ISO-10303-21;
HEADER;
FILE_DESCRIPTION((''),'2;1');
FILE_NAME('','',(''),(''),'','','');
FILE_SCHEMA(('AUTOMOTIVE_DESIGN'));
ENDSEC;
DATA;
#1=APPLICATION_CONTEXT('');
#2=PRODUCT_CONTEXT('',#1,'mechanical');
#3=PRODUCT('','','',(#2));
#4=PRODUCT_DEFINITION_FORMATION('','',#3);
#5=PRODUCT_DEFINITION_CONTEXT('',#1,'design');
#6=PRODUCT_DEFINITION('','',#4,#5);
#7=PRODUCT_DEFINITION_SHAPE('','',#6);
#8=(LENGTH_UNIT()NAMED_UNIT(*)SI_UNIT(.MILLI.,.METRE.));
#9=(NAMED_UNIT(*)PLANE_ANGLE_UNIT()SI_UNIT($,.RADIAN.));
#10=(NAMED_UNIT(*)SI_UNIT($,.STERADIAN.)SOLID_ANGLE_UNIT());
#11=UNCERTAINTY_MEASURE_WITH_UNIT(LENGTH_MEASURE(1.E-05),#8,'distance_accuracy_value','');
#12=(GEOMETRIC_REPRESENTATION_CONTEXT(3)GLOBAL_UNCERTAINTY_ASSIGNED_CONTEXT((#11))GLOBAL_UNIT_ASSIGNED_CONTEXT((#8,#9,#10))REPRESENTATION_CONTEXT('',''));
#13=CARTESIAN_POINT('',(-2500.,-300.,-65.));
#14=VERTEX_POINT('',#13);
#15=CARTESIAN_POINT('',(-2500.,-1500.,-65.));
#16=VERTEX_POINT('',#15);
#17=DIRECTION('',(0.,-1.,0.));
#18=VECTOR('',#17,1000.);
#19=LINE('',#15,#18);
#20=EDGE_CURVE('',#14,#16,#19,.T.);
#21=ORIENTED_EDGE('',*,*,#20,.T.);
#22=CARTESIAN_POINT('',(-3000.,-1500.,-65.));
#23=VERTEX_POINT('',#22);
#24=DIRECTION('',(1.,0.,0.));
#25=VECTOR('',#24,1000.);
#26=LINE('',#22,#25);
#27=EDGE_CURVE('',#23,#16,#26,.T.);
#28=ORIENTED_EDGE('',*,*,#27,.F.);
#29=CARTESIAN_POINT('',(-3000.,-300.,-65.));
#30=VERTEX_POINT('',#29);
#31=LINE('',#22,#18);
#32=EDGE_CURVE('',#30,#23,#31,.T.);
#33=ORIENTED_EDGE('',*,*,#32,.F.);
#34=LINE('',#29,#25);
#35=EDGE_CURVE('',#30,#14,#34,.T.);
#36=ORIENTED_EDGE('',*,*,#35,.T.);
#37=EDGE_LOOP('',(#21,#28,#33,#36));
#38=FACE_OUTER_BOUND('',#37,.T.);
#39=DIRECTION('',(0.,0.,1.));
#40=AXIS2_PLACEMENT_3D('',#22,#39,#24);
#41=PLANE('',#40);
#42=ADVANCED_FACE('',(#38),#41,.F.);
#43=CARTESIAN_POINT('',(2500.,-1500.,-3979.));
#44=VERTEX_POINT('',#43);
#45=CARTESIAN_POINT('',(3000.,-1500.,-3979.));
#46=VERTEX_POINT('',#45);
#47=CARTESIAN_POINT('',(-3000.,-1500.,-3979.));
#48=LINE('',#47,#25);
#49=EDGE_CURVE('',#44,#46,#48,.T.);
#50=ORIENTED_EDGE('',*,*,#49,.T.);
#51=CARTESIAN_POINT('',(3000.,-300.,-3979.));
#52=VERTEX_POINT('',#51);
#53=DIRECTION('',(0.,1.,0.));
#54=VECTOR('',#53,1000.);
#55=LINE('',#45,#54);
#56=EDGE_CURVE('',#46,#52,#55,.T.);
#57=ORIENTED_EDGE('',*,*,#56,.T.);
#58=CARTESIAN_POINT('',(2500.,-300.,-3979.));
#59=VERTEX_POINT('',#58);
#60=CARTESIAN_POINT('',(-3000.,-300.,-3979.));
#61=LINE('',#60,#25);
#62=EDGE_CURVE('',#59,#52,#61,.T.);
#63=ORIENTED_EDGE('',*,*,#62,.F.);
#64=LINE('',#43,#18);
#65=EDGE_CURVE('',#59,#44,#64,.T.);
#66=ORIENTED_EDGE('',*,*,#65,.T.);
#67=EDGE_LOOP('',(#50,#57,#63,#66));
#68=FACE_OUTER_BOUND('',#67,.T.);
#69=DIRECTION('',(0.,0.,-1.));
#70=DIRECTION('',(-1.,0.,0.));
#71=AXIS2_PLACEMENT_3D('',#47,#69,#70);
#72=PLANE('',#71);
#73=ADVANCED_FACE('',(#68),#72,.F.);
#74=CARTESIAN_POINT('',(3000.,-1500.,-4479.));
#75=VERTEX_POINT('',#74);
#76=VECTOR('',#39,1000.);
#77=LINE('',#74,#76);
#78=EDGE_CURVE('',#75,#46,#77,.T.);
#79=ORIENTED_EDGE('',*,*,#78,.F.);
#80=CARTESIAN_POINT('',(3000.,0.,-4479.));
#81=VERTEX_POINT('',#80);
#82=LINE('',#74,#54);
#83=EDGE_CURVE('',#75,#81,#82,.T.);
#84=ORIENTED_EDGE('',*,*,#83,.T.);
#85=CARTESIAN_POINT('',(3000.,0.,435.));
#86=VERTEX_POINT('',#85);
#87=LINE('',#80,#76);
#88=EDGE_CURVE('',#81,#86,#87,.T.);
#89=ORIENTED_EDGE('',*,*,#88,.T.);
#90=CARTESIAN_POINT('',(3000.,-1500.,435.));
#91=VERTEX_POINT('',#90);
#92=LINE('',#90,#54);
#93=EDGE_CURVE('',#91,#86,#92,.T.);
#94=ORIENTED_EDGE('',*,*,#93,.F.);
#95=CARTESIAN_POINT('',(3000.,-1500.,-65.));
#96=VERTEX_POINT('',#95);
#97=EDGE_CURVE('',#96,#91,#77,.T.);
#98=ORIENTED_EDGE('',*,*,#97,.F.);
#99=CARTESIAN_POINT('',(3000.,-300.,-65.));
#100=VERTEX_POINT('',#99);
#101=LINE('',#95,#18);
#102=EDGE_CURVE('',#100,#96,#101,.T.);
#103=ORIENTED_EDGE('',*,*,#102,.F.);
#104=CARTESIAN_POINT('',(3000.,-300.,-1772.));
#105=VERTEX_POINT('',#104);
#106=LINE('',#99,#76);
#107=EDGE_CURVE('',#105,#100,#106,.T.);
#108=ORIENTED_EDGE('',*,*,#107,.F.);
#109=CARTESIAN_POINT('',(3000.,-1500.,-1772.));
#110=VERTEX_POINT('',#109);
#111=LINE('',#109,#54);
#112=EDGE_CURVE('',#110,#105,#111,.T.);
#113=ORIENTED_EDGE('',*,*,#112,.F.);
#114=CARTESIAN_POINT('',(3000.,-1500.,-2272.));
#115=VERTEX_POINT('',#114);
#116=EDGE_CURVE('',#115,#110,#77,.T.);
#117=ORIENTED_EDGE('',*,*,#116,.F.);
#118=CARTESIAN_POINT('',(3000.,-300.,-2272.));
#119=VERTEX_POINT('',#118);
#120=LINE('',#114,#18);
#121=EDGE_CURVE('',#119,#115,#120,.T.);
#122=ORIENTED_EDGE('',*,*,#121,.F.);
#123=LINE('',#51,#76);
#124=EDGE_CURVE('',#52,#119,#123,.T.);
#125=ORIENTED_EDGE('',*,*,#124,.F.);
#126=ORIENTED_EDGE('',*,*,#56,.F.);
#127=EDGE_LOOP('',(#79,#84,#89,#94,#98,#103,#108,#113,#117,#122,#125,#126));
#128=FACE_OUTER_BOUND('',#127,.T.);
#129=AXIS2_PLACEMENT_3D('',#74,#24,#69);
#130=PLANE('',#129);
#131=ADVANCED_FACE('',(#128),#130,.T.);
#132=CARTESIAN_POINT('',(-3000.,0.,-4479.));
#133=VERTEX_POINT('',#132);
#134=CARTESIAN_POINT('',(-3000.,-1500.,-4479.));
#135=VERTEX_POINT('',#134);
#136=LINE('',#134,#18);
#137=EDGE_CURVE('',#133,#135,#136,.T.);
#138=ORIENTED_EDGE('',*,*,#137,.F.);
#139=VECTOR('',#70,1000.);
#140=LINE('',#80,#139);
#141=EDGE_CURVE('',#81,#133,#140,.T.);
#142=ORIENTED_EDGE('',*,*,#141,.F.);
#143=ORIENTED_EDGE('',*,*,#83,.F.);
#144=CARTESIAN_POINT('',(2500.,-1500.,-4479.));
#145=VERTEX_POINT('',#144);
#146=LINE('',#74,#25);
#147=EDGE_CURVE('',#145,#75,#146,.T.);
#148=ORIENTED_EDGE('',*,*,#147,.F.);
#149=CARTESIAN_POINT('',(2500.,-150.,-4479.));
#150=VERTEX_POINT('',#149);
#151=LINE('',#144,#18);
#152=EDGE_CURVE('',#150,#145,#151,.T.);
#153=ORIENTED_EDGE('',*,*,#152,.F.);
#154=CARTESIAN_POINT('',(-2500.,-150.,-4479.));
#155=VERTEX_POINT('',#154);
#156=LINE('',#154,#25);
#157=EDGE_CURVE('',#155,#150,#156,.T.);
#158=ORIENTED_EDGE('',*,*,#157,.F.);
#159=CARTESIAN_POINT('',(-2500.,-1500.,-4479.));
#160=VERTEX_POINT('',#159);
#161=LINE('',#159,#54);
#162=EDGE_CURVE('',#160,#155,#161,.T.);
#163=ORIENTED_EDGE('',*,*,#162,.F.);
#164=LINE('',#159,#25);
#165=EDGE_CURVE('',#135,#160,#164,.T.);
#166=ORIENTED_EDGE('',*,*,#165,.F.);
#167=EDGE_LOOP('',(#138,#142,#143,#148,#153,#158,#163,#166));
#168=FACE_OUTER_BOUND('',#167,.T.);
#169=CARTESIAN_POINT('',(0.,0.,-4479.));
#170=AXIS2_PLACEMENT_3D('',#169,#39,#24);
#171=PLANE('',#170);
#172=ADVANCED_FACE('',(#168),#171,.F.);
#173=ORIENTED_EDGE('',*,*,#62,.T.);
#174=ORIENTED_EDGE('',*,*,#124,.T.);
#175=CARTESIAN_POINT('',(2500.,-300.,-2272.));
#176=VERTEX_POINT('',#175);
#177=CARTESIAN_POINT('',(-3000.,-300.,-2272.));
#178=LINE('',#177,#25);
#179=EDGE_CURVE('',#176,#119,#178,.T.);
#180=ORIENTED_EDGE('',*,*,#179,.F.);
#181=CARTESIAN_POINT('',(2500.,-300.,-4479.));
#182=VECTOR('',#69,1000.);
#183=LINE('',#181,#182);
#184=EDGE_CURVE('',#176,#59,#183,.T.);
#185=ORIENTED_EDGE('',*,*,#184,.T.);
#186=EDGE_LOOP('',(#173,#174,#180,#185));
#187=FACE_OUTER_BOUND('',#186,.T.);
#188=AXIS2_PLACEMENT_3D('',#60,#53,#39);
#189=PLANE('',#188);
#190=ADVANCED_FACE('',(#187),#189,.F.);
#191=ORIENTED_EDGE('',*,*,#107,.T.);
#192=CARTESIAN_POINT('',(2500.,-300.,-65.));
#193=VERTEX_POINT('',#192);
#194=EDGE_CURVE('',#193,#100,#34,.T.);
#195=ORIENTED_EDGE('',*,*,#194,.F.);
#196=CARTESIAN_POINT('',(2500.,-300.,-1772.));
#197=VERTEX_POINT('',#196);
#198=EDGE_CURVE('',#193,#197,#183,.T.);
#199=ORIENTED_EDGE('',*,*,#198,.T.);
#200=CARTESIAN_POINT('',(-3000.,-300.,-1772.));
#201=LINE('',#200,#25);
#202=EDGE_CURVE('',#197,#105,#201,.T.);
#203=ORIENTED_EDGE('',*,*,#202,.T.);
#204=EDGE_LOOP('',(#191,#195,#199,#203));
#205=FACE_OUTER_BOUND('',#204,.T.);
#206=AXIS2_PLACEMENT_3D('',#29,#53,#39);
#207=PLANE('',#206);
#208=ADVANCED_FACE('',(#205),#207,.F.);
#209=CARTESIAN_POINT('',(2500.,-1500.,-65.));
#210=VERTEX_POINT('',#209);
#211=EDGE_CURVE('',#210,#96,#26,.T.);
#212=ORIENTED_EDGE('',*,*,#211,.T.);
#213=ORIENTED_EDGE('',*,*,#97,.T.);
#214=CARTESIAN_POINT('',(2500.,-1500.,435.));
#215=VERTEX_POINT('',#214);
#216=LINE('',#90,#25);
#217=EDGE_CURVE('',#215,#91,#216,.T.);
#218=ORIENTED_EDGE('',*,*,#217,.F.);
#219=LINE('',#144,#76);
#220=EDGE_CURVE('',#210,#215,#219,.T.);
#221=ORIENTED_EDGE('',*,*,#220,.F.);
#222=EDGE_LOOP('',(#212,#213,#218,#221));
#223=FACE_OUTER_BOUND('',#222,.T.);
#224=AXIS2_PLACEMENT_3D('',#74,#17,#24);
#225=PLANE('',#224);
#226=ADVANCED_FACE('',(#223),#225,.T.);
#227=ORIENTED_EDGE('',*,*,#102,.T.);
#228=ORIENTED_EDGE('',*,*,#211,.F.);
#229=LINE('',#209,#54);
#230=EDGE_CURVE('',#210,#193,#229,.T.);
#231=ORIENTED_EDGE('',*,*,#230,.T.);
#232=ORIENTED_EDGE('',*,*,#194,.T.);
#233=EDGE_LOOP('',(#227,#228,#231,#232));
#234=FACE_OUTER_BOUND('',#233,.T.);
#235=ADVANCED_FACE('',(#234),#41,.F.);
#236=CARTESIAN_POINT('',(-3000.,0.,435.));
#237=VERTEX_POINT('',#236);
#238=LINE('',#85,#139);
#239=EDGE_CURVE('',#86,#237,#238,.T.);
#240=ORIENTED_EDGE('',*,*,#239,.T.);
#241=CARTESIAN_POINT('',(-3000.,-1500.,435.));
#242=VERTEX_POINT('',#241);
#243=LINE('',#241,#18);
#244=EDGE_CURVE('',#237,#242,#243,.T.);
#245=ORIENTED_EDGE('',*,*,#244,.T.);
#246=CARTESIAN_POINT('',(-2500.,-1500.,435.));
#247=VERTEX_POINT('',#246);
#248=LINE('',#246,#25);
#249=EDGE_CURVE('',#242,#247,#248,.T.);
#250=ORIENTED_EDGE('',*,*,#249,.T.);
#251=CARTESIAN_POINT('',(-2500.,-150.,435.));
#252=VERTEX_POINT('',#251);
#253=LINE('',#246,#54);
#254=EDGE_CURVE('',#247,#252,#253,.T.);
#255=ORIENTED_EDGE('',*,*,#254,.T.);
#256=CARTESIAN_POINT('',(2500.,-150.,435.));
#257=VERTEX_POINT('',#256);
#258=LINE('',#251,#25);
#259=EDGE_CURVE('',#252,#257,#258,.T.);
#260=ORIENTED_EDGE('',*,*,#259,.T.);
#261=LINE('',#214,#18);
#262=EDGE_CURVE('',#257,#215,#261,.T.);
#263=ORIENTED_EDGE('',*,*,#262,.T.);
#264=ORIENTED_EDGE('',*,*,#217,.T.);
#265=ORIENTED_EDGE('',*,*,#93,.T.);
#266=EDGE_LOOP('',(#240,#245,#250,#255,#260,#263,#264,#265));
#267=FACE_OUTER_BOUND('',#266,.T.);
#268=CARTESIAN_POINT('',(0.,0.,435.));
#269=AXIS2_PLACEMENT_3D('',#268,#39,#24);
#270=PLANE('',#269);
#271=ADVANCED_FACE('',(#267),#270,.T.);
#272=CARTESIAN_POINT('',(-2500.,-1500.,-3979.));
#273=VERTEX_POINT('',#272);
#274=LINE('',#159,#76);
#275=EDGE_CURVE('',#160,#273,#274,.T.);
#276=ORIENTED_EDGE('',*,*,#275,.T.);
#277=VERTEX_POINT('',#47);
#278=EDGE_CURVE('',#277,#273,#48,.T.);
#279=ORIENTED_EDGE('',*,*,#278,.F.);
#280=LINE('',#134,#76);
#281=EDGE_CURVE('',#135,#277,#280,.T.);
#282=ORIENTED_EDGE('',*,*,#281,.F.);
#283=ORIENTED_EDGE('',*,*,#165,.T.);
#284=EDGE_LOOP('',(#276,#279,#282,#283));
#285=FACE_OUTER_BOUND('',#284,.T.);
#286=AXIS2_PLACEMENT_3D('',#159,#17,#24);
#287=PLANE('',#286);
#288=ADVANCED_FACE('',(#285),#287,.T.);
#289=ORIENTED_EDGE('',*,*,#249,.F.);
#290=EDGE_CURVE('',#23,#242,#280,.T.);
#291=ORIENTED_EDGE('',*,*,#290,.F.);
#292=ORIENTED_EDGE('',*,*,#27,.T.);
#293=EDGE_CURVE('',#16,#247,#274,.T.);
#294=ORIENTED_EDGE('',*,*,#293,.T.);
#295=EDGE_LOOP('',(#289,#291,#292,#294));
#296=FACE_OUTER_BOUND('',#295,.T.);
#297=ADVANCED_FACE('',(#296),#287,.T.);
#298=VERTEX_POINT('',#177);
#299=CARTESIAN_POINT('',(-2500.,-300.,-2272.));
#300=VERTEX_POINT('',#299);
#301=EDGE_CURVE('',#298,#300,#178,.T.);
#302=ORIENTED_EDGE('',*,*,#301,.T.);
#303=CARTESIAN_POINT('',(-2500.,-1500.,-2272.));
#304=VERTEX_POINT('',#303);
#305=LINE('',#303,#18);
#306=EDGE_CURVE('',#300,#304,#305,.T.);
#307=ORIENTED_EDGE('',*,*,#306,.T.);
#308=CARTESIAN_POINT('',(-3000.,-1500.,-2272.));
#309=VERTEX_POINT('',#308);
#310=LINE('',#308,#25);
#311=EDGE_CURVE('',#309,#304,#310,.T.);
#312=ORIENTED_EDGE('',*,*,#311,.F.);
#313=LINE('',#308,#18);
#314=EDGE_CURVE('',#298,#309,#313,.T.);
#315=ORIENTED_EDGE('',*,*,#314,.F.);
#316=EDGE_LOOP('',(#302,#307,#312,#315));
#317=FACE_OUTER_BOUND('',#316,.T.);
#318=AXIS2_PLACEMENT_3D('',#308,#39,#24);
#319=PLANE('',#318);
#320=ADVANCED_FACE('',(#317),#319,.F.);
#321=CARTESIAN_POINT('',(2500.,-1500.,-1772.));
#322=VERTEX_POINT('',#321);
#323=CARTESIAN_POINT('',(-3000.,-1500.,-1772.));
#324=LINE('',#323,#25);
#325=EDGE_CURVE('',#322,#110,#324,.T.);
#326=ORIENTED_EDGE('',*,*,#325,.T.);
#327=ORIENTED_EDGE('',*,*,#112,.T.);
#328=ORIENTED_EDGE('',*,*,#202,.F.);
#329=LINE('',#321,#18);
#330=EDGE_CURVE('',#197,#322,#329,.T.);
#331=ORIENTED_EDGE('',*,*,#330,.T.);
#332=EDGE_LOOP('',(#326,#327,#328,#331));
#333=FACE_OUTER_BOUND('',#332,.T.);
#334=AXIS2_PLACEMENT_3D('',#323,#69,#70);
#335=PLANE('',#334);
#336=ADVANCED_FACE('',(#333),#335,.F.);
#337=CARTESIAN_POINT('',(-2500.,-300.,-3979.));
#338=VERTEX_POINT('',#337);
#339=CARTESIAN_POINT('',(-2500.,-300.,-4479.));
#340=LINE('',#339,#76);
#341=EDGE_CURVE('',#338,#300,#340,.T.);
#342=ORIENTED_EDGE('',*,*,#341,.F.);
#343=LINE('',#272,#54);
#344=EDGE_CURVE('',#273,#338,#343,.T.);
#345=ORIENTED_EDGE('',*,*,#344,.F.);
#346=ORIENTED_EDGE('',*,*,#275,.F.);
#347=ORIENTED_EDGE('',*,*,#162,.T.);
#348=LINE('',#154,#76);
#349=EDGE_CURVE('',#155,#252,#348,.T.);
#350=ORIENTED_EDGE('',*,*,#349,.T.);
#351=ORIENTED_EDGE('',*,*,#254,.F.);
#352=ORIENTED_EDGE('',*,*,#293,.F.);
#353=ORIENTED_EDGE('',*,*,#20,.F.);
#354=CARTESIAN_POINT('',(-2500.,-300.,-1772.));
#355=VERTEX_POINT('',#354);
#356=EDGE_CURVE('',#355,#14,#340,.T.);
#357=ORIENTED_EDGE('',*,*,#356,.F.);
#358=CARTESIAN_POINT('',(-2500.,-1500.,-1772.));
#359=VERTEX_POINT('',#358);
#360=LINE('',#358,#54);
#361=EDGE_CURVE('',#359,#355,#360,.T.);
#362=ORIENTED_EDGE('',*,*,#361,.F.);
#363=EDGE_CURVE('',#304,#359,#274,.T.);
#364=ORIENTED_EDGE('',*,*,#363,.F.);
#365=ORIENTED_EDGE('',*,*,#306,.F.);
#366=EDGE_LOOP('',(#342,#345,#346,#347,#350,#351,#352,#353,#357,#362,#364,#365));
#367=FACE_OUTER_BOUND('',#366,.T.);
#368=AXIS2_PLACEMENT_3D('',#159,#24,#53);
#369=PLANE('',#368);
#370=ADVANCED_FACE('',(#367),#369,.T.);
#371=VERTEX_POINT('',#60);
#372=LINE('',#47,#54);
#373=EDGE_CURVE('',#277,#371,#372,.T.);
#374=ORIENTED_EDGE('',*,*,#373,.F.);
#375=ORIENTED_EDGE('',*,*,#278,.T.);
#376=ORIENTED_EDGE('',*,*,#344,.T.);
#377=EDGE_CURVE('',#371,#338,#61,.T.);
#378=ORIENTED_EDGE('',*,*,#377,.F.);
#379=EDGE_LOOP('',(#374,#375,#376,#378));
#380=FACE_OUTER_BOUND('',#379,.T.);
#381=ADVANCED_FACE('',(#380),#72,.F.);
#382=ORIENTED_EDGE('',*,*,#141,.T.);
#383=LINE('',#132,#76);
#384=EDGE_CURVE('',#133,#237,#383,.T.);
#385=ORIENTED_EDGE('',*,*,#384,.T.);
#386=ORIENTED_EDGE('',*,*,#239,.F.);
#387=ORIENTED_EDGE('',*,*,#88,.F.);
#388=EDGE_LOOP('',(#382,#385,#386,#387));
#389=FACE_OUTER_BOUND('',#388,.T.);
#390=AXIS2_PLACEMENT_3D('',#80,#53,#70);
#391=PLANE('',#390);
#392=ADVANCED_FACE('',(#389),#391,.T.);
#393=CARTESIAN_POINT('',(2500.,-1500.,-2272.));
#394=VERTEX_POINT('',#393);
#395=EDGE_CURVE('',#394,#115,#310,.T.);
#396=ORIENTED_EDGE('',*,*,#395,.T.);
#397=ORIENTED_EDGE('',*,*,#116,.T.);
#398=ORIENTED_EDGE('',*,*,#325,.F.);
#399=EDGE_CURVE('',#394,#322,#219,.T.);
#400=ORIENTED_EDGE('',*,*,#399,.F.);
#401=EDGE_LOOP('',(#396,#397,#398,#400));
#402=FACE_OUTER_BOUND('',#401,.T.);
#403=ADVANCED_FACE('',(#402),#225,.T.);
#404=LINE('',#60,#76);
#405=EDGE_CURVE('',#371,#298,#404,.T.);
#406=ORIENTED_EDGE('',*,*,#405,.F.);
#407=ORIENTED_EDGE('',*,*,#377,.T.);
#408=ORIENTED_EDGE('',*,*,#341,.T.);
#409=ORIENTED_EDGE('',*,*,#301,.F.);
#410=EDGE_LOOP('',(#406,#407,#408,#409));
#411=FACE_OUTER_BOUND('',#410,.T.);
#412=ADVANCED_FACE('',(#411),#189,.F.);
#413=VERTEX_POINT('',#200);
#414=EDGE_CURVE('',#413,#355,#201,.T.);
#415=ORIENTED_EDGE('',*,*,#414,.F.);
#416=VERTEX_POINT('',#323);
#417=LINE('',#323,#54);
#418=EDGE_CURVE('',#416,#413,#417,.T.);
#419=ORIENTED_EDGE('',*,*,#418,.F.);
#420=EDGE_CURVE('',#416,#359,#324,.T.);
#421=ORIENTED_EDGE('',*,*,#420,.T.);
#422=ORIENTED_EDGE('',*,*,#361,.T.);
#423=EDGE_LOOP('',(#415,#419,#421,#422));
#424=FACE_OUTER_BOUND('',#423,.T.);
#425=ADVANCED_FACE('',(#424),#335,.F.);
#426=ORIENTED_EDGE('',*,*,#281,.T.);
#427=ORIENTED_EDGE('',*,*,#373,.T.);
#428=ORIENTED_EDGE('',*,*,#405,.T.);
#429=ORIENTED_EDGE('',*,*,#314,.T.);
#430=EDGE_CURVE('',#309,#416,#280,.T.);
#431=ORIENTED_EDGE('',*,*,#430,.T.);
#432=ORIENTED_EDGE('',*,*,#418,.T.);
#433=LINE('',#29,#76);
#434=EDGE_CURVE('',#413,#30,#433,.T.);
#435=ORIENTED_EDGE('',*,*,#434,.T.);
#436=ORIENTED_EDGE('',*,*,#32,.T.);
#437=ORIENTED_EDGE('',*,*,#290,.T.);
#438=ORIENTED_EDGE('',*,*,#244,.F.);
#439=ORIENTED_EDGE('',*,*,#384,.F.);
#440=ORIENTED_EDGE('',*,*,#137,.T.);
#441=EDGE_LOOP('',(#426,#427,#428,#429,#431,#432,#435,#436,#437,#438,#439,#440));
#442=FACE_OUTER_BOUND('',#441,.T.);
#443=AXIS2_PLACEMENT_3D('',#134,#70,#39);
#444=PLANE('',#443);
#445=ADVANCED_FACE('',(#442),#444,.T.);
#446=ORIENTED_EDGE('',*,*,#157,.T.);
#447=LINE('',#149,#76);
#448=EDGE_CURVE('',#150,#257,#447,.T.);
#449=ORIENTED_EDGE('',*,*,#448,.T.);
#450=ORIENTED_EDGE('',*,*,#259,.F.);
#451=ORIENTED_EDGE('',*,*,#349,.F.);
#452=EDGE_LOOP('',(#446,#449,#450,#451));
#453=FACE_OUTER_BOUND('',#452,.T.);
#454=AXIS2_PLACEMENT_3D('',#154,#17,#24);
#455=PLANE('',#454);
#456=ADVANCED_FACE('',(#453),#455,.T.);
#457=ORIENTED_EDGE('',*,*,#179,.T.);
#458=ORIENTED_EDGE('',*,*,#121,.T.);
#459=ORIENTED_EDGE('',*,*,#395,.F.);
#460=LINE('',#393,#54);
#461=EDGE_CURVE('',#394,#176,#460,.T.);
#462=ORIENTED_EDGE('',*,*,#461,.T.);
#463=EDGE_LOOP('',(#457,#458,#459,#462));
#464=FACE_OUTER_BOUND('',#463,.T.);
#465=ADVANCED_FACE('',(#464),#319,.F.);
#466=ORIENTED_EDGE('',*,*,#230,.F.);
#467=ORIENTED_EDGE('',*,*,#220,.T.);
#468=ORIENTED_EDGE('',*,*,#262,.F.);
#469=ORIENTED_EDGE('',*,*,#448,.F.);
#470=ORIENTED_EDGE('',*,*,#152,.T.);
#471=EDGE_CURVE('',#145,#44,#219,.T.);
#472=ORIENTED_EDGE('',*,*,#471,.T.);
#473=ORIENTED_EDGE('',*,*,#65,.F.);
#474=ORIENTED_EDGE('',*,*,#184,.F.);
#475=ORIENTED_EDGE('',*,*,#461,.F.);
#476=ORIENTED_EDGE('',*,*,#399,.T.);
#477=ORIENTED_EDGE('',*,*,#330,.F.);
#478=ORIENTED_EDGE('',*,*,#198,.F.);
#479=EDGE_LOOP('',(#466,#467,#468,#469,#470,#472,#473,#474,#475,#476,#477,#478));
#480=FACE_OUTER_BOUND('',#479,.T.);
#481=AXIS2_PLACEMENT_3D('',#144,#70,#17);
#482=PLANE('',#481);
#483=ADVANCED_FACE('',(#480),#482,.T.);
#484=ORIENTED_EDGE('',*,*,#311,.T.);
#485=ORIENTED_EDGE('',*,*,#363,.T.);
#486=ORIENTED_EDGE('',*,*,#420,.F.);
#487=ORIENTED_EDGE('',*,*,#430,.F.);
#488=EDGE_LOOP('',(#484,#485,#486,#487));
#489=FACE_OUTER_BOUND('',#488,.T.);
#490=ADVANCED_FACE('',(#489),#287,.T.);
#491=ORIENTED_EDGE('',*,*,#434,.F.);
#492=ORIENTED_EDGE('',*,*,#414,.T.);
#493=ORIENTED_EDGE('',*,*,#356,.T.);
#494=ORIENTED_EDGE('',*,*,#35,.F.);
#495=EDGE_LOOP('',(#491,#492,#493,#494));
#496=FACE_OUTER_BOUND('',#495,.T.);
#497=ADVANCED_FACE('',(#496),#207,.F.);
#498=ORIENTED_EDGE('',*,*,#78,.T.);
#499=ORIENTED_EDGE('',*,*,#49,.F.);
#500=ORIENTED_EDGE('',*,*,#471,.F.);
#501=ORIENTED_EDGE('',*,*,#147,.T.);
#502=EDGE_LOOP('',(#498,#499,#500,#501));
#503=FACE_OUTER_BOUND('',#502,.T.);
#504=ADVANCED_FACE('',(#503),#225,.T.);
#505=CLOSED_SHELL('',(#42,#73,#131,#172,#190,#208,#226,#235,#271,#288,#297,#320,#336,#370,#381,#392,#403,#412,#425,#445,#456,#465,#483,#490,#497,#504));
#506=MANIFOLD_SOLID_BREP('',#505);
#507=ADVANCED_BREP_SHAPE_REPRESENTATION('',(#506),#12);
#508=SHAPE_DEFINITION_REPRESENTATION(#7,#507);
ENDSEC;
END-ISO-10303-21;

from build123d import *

# Parameters (mm, degrees)
BOSS_EXTRUDE1_DEPTH      = 435
BOSS_EXTRUDE1_DEPTH_BACK = 4479
SKETCH3_W                = 1707
SKETCH3_H                = 1200
CUT_EXTRUDE1_DEPTH       = 7637.192834129


with BuildPart() as part:
    # Sketch2 → Boss-Extrude1 (new, two sides: drawn at the far end of the back side and taken through both)
    with BuildSketch(Plane.XY.offset(-BOSS_EXTRUDE1_DEPTH_BACK)):
        Polygon((3000, -1500), (2500, -1500), (2500, -150), (-2500, -150), (-2500, -1500), (-3000, -1500), (-3000, 0), (3000, 0), align=None)
    extrude(amount=BOSS_EXTRUDE1_DEPTH + BOSS_EXTRUDE1_DEPTH_BACK)

    # Sketch3 → Cut-Extrude1 (cut, through all)
    with BuildSketch(Plane(origin=(3000, 0, 0), x_dir=(0, 0, -1), z_dir=(1, 0, 0))):
        with Locations((918.5, -900)):
            Rectangle(SKETCH3_W, SKETCH3_H)
        with Locations((3125.5, -900)):
            Rectangle(SKETCH3_W, SKETCH3_H)
    extrude(amount=-CUT_EXTRUDE1_DEPTH, mode=Mode.SUBTRACT)


solid = part.part
